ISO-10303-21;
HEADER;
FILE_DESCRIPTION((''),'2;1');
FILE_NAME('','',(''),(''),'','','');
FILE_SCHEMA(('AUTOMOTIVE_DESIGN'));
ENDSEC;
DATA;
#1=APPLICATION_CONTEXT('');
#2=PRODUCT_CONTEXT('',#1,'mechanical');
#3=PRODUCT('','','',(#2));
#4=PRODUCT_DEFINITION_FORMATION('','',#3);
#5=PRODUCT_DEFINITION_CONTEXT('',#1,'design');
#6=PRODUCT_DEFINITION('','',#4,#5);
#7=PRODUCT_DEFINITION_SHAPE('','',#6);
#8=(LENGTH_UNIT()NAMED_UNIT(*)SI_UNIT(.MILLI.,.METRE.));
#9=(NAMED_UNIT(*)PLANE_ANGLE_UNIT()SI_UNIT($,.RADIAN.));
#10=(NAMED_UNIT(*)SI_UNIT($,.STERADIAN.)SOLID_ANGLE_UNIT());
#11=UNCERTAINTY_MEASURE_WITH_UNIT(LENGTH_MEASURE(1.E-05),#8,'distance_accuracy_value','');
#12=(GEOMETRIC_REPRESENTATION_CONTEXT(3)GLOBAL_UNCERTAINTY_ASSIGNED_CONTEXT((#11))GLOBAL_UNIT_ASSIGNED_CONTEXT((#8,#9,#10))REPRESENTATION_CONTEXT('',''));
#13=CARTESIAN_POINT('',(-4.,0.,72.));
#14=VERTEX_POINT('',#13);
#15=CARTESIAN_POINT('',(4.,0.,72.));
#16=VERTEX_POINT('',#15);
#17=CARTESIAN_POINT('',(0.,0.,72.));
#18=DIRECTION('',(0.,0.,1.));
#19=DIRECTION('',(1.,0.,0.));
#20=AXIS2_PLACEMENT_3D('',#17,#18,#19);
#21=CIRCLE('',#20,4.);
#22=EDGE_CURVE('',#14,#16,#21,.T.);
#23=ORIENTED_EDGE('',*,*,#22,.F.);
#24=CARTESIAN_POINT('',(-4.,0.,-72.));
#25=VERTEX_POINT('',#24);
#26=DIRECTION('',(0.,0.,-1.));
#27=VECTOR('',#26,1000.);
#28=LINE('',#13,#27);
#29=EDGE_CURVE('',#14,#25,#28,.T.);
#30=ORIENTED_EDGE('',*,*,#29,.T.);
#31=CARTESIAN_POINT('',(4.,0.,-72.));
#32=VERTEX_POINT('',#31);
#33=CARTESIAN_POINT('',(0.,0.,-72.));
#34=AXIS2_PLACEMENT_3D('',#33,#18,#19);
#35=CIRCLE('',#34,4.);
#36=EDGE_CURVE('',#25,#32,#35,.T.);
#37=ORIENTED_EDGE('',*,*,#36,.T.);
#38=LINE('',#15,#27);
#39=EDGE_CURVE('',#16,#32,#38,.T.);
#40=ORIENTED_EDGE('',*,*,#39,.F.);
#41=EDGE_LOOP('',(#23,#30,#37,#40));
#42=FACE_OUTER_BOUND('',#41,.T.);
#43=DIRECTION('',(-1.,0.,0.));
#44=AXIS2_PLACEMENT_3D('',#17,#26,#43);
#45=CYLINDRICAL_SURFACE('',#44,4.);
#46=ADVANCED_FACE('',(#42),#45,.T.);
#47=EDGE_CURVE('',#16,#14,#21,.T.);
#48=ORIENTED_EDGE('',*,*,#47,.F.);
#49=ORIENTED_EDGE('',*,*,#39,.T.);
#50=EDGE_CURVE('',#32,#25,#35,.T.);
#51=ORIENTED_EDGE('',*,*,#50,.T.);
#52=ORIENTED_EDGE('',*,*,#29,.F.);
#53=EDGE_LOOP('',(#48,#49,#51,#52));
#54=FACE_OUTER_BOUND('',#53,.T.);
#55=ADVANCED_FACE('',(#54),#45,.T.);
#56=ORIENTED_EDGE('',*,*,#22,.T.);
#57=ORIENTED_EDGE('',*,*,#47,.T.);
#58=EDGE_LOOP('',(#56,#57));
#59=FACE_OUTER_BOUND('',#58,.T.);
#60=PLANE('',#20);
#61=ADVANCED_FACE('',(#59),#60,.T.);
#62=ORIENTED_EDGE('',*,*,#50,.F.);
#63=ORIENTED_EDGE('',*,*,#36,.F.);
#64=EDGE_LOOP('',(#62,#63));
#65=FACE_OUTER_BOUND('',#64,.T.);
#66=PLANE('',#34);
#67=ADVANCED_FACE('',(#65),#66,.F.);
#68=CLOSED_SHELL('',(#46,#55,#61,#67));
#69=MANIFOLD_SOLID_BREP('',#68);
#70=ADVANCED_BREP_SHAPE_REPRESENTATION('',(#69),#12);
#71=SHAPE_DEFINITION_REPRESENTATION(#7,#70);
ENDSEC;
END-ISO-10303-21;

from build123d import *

# Parameters (mm, degrees)
SKETCH_1_R      = 4
EXTRUDE_1_DEPTH = 72


with BuildPart() as part:
    # 草图1 → 凸台-拉伸1 (new, symmetric)
    with BuildSketch(Plane.XY):
        Circle(SKETCH_1_R)
    extrude(amount=EXTRUDE_1_DEPTH, both=True)


solid = part.part
